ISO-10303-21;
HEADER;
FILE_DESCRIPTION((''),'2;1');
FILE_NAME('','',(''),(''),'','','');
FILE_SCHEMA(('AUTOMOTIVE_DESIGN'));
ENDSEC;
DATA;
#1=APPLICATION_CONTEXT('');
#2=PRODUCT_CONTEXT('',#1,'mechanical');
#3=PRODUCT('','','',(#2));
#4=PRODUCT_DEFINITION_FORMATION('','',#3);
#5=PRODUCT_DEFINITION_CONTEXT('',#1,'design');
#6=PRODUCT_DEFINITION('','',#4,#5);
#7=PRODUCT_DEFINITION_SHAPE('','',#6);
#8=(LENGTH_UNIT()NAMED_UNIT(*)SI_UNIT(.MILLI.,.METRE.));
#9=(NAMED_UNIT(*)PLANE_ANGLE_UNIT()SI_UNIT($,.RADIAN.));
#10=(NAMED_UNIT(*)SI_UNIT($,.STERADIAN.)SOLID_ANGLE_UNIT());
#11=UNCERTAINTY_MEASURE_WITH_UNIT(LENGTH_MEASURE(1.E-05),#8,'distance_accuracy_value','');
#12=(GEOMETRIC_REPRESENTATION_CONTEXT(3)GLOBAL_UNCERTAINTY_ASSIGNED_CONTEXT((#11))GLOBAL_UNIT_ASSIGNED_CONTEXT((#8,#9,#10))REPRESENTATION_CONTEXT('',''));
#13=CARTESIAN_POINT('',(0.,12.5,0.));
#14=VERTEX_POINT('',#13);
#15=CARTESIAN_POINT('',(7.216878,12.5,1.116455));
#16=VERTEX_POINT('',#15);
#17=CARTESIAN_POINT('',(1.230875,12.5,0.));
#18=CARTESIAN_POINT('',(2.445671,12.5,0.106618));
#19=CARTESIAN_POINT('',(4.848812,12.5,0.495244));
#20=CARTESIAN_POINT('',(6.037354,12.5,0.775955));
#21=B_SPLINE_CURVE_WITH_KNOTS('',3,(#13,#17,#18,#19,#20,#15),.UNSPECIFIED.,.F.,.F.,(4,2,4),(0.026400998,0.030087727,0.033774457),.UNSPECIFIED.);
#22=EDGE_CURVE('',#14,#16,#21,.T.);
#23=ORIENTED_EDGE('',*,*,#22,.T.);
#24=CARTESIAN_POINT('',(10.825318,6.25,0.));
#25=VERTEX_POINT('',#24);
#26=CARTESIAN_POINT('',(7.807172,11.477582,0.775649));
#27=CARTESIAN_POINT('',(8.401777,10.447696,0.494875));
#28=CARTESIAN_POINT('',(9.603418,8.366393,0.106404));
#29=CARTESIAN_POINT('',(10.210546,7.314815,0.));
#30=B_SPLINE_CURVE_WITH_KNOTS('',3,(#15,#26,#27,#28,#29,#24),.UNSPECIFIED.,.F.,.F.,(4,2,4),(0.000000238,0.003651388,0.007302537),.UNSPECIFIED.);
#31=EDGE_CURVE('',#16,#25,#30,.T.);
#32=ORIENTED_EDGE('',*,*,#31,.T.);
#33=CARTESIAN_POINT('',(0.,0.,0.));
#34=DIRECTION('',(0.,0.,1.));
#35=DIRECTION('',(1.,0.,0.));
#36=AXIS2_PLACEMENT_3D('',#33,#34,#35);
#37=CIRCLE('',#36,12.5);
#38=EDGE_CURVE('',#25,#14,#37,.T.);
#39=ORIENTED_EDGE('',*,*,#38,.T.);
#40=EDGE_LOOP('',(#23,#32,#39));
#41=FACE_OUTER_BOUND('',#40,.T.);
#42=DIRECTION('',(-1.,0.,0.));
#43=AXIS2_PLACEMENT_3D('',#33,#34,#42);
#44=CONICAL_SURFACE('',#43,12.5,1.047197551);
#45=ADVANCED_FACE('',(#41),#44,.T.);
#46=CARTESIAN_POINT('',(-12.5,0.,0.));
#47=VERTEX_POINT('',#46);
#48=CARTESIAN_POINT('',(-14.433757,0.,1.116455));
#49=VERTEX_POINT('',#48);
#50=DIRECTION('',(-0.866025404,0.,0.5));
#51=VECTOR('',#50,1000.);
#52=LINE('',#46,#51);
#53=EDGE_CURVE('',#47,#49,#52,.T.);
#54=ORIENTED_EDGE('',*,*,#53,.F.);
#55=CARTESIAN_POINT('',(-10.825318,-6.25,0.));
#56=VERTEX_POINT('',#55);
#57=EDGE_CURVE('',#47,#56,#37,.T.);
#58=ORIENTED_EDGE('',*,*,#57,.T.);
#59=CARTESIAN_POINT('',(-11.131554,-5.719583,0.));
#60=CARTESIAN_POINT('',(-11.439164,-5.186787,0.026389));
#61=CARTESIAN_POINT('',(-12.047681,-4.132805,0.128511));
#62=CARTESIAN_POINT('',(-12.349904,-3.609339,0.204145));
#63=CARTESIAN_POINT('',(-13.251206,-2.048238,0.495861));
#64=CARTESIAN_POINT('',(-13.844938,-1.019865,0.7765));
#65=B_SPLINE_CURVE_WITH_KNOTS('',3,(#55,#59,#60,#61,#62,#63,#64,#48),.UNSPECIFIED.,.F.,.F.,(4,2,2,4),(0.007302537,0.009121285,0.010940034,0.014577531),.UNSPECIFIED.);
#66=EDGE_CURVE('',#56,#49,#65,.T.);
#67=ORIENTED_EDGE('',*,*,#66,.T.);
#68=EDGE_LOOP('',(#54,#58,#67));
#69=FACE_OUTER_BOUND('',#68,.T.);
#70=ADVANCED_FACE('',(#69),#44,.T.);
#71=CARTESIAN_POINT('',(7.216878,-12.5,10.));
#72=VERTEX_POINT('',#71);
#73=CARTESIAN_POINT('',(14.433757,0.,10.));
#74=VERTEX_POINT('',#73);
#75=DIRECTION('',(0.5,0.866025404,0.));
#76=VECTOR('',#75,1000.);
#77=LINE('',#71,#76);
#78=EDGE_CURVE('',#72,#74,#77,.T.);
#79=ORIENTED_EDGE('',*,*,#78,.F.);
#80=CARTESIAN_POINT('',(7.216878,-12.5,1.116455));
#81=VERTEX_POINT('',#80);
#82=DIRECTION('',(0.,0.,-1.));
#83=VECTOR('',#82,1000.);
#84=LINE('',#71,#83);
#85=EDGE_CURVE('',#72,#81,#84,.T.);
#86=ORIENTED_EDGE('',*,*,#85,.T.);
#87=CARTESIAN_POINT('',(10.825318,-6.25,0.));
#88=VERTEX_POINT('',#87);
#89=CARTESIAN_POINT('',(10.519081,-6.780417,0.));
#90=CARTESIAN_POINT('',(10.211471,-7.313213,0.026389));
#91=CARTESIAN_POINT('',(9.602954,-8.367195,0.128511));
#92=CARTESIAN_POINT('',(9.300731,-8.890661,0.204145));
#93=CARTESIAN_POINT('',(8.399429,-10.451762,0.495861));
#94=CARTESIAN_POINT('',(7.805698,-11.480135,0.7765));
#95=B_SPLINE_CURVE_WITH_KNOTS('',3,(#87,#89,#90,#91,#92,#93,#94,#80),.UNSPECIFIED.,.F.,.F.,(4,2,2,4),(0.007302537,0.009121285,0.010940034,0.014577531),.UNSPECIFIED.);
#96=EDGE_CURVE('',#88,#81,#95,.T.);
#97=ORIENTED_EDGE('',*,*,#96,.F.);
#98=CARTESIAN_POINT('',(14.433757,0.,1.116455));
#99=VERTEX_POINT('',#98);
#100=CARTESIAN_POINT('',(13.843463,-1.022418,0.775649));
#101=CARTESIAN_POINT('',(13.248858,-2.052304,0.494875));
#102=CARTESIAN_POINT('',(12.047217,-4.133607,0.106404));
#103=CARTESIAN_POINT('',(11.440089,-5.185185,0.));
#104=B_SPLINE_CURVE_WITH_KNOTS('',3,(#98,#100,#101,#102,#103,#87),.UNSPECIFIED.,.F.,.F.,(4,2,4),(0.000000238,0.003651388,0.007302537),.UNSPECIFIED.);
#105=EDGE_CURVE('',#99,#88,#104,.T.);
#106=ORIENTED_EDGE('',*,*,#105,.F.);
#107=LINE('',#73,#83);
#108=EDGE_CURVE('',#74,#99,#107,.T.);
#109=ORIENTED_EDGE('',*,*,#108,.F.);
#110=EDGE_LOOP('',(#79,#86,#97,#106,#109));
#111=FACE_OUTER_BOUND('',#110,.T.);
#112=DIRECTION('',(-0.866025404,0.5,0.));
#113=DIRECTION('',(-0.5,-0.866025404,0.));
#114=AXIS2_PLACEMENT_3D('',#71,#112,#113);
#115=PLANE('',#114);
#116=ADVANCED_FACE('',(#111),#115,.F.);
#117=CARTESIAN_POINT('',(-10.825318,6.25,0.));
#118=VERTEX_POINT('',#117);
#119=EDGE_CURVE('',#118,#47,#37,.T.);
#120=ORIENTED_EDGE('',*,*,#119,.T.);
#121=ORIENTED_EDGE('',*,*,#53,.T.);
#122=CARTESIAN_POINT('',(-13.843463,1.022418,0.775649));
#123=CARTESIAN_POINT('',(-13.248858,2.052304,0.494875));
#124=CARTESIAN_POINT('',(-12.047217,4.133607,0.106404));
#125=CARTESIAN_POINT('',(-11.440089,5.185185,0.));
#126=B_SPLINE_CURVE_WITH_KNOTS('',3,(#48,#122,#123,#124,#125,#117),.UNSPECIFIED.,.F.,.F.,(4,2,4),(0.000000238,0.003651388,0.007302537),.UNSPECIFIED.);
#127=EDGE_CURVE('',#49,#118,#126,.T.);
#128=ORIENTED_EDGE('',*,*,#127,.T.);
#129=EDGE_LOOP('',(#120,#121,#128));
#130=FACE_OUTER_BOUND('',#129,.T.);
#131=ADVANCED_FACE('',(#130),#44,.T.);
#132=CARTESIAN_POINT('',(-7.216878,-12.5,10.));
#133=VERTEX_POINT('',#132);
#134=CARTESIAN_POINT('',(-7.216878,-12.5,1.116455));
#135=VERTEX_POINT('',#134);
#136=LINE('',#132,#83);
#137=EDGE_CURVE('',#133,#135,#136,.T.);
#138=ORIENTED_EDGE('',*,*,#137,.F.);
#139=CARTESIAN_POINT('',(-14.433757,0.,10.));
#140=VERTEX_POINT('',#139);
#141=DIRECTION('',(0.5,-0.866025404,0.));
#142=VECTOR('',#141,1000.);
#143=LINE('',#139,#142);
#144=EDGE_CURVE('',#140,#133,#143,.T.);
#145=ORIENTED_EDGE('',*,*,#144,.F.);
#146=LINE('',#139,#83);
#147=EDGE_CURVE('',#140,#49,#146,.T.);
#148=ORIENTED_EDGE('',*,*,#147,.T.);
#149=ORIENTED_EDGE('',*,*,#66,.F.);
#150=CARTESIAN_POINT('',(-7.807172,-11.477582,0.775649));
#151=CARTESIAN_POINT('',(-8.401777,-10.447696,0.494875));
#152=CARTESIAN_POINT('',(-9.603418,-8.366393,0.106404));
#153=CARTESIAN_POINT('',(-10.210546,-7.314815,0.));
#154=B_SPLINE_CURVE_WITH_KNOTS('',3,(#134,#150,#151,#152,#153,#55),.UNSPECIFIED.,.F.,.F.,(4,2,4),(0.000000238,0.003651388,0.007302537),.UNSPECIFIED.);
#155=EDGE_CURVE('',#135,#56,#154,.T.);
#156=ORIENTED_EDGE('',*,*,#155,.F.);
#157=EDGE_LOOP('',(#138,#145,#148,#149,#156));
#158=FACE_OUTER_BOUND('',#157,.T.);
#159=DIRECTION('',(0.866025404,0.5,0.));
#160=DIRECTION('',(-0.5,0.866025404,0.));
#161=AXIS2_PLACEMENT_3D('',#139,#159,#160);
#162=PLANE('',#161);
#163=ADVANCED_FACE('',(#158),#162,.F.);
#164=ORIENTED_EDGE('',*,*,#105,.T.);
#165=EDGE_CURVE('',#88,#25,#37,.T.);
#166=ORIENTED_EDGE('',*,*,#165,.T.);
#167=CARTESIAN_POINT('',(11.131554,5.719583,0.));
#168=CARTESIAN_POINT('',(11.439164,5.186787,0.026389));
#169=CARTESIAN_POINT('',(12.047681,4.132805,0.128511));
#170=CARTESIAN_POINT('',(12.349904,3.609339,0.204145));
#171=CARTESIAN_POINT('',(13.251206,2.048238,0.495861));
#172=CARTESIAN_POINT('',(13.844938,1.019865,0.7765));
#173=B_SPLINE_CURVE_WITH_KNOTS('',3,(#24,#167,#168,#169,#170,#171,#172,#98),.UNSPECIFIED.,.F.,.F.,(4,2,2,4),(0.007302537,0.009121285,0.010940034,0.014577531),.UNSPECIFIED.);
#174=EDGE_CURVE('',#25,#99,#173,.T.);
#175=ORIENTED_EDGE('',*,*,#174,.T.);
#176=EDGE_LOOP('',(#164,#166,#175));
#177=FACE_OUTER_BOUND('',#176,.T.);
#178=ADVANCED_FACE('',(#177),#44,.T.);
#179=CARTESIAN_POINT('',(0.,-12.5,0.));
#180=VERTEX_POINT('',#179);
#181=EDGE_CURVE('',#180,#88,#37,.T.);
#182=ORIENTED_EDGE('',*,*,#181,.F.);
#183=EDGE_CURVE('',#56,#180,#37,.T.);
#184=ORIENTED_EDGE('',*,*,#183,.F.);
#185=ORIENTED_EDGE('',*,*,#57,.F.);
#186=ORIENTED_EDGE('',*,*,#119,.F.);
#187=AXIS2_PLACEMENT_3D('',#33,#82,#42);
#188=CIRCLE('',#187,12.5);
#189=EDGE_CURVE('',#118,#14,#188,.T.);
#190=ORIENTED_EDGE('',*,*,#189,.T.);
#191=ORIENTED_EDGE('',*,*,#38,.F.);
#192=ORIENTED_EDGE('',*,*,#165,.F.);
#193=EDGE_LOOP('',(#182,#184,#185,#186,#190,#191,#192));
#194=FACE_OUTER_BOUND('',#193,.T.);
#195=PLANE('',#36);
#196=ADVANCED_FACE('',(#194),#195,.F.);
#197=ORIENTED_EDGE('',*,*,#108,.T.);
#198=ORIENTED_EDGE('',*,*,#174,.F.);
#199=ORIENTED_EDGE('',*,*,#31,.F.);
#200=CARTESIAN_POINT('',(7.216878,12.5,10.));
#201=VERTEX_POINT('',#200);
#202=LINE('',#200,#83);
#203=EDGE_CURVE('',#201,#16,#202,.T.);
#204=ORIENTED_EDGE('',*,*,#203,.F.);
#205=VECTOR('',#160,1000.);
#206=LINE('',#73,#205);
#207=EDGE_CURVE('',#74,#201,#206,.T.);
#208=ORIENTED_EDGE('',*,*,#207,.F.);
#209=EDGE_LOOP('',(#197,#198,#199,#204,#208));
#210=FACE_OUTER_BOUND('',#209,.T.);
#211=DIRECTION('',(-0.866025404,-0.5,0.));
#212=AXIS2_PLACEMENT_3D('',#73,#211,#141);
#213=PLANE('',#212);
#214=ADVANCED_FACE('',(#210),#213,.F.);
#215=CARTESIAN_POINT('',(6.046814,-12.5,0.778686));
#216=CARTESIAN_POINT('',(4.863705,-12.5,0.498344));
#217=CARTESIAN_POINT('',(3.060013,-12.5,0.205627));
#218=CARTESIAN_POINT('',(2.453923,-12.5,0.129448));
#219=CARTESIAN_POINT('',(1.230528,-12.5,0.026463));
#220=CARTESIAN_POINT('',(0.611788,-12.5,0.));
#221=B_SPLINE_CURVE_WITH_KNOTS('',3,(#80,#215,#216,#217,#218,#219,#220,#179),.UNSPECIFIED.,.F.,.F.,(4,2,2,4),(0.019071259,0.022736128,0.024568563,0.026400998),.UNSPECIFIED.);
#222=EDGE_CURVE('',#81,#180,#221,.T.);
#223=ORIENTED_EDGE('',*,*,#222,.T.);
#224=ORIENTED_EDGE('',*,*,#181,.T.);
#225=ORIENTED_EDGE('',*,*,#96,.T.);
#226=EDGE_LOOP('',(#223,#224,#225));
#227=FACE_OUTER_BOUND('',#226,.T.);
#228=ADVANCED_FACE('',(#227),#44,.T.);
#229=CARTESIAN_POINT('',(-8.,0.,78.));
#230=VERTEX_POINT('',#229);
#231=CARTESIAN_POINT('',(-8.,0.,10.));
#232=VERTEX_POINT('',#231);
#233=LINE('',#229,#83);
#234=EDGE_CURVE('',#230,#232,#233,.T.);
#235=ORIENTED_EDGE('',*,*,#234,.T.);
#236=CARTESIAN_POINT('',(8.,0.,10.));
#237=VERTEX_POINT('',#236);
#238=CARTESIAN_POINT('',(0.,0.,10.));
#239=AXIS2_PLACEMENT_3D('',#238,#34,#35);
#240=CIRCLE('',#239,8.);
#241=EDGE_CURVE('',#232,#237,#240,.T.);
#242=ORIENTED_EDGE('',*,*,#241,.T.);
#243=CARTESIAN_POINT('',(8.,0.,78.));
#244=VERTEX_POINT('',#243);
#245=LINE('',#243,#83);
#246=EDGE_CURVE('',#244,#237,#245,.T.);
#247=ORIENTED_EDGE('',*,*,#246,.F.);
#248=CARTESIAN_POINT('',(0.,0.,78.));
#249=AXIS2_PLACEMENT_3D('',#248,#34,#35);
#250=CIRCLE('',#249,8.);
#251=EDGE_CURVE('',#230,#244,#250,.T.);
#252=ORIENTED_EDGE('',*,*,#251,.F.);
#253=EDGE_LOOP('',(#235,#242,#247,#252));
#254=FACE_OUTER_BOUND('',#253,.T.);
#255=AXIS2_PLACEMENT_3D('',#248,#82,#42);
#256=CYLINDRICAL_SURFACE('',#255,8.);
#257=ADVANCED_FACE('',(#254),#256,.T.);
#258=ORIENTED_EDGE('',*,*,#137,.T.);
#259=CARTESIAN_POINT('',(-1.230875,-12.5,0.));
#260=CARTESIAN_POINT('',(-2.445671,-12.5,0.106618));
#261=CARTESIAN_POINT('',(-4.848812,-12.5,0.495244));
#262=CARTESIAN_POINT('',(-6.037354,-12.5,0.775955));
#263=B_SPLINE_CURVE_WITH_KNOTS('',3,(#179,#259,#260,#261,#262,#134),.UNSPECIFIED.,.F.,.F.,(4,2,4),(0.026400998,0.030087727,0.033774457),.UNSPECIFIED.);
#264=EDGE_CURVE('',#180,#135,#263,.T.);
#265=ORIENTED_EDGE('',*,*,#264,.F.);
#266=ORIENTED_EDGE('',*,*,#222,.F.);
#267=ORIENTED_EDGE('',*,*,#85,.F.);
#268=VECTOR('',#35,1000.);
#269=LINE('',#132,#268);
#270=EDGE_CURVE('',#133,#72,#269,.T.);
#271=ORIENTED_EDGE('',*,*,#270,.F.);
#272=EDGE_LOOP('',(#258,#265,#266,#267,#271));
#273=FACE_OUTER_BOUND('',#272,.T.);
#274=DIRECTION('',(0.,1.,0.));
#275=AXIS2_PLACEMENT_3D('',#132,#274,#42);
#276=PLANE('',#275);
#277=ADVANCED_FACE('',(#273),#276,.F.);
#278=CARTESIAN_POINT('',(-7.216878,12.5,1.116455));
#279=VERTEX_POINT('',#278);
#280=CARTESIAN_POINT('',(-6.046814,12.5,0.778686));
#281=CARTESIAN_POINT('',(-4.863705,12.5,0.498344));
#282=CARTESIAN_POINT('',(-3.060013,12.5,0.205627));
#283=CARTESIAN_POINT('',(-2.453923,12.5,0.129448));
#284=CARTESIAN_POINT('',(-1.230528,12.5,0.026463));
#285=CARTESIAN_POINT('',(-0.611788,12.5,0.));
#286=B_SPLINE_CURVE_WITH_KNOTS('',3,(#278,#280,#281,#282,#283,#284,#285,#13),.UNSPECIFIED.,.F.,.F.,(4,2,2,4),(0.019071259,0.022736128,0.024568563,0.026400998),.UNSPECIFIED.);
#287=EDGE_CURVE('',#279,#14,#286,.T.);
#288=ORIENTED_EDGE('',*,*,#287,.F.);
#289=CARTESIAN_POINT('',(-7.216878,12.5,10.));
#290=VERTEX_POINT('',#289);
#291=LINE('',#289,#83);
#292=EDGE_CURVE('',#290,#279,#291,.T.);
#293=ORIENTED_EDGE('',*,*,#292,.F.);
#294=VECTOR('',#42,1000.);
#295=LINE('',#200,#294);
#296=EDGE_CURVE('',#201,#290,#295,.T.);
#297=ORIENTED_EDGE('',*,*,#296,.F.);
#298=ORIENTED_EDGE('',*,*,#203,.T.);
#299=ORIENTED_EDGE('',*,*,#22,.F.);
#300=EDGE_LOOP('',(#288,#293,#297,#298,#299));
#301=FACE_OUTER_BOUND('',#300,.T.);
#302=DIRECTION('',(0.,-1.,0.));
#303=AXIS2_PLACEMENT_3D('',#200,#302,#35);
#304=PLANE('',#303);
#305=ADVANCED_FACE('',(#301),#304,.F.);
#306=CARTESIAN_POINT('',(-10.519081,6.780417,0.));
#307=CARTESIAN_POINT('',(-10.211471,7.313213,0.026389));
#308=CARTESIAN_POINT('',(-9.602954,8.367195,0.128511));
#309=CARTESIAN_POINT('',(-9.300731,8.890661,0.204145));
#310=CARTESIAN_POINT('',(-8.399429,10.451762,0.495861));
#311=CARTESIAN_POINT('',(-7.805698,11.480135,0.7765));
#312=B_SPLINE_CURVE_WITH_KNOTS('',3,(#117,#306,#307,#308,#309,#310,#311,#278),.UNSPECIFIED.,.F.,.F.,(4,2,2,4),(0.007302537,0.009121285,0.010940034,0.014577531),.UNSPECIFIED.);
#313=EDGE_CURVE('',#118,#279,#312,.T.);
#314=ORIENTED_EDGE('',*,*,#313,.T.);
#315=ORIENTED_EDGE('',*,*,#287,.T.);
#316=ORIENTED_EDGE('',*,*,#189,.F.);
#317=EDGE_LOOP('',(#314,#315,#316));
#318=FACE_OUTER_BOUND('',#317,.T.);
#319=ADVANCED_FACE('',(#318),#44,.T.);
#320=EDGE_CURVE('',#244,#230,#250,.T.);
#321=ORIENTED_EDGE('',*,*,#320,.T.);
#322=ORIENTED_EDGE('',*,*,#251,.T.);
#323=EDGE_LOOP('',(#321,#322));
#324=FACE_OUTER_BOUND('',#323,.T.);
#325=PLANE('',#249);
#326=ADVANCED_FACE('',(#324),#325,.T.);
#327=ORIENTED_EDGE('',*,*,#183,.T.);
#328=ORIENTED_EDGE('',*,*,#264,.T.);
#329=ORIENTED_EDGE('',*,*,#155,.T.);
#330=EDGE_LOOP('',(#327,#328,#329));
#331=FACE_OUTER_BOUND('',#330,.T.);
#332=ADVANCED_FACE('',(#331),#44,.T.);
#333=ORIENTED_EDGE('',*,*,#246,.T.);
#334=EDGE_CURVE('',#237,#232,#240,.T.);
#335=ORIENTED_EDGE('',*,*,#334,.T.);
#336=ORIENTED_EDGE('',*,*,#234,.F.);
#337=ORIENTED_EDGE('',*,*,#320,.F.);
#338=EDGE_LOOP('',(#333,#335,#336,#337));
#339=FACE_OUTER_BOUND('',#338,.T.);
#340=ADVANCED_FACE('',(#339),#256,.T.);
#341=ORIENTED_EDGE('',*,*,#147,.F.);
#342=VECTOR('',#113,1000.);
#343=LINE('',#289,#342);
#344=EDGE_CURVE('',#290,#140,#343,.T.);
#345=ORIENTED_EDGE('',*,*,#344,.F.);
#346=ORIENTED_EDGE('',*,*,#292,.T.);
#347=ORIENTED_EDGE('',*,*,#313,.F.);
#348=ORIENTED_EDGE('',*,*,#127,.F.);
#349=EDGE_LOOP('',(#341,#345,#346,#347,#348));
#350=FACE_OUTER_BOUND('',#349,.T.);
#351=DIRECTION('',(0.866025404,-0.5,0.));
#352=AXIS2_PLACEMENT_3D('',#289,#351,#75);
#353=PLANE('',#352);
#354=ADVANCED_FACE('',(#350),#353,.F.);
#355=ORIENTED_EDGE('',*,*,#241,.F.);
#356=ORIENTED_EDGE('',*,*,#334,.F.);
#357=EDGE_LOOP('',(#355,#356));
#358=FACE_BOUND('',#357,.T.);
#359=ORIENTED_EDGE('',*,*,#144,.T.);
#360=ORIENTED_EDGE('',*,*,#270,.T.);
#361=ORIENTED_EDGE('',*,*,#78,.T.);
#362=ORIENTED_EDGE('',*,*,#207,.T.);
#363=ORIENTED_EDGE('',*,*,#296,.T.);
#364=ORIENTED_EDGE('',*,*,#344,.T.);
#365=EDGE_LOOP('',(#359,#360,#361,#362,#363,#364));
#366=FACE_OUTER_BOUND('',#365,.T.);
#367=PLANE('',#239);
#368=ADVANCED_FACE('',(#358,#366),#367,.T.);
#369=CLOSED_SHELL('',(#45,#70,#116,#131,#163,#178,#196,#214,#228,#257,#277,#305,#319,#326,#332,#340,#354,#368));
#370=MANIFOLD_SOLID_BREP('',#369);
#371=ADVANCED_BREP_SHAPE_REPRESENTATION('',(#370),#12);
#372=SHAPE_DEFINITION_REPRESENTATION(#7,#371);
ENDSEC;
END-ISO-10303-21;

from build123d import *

# Parameters (mm, degrees)
HEX_HEAD_25AF_X10_DEPTH        = 10
HEAD_CHAMFER_PROFILE_OUTSIDE_W = 73.404
HEAD_CHAMFER_PROFILE_OUTSIDE_H = 69.536
HEAD_CHAMFER_PROFILE_OUTSIDE_R = 12.5
HEAD_CHAMFER_CUT_DEPTH         = 10
HEAD_CHAMFER_CUT_DRAFT         = -60
SHANK_PROFILE_16_R             = 8
SHANK_16_X68_DEPTH             = 68


with BuildPart() as part:
    # Hex Head Profile 25AF → Hex Head 25AF x10 (new body)
    with BuildSketch(Plane.XY):
        Polygon((14.43375673, 0), (7.216878365, 12.5), (-7.216878365, 12.5), (-14.43375673, 0), (-7.216878365, -12.5), (7.216878365, -12.5), align=None)
    extrude(amount=HEX_HEAD_25AF_X10_DEPTH)


with BuildPart() as head_chamfer_cut_tool:
    # Head Chamfer Profile outside → Head Chamfer Cut (with draft: the straight prism first)
    with BuildSketch(Plane(origin=(0, 0, 0), x_dir=(-1, 0, 0), z_dir=(0, 0, -1))):
        Rectangle(HEAD_CHAMFER_PROFILE_OUTSIDE_W, HEAD_CHAMFER_PROFILE_OUTSIDE_H)
        Circle(HEAD_CHAMFER_PROFILE_OUTSIDE_R, mode=Mode.SUBTRACT)
    extrude(amount=-HEAD_CHAMFER_CUT_DEPTH)
    # Head Chamfer Cut: the draft: its side faces are tilted about the plane it starts from
    head_chamfer_cut_sides = [head_chamfer_cut_tool.faces().sort_by_distance(p)[0] for p in [
        (0, -34.768, 5),
        (-36.702, 0, 5),
        (0, 34.768, 5),
        (36.702, 0, 5),
        (12.5, 0, 5),
    ]]
    draft(head_chamfer_cut_sides, Plane(origin=(0, 0, 0), x_dir=(-1, 0, 0), z_dir=(0, 0, -1)), HEAD_CHAMFER_CUT_DRAFT)


with BuildPart() as part_1:
    add(part.part)

    # Head Chamfer Cut: cut by head_chamfer_cut_tool
    add(head_chamfer_cut_tool.part, mode=Mode.SUBTRACT)

    # Shank Profile Ø16 → Shank Ø16 x68 (add)
    with BuildSketch(Plane.XY.offset(10)):
        Circle(SHANK_PROFILE_16_R)
    extrude(amount=SHANK_16_X68_DEPTH)


solid = part_1.part
